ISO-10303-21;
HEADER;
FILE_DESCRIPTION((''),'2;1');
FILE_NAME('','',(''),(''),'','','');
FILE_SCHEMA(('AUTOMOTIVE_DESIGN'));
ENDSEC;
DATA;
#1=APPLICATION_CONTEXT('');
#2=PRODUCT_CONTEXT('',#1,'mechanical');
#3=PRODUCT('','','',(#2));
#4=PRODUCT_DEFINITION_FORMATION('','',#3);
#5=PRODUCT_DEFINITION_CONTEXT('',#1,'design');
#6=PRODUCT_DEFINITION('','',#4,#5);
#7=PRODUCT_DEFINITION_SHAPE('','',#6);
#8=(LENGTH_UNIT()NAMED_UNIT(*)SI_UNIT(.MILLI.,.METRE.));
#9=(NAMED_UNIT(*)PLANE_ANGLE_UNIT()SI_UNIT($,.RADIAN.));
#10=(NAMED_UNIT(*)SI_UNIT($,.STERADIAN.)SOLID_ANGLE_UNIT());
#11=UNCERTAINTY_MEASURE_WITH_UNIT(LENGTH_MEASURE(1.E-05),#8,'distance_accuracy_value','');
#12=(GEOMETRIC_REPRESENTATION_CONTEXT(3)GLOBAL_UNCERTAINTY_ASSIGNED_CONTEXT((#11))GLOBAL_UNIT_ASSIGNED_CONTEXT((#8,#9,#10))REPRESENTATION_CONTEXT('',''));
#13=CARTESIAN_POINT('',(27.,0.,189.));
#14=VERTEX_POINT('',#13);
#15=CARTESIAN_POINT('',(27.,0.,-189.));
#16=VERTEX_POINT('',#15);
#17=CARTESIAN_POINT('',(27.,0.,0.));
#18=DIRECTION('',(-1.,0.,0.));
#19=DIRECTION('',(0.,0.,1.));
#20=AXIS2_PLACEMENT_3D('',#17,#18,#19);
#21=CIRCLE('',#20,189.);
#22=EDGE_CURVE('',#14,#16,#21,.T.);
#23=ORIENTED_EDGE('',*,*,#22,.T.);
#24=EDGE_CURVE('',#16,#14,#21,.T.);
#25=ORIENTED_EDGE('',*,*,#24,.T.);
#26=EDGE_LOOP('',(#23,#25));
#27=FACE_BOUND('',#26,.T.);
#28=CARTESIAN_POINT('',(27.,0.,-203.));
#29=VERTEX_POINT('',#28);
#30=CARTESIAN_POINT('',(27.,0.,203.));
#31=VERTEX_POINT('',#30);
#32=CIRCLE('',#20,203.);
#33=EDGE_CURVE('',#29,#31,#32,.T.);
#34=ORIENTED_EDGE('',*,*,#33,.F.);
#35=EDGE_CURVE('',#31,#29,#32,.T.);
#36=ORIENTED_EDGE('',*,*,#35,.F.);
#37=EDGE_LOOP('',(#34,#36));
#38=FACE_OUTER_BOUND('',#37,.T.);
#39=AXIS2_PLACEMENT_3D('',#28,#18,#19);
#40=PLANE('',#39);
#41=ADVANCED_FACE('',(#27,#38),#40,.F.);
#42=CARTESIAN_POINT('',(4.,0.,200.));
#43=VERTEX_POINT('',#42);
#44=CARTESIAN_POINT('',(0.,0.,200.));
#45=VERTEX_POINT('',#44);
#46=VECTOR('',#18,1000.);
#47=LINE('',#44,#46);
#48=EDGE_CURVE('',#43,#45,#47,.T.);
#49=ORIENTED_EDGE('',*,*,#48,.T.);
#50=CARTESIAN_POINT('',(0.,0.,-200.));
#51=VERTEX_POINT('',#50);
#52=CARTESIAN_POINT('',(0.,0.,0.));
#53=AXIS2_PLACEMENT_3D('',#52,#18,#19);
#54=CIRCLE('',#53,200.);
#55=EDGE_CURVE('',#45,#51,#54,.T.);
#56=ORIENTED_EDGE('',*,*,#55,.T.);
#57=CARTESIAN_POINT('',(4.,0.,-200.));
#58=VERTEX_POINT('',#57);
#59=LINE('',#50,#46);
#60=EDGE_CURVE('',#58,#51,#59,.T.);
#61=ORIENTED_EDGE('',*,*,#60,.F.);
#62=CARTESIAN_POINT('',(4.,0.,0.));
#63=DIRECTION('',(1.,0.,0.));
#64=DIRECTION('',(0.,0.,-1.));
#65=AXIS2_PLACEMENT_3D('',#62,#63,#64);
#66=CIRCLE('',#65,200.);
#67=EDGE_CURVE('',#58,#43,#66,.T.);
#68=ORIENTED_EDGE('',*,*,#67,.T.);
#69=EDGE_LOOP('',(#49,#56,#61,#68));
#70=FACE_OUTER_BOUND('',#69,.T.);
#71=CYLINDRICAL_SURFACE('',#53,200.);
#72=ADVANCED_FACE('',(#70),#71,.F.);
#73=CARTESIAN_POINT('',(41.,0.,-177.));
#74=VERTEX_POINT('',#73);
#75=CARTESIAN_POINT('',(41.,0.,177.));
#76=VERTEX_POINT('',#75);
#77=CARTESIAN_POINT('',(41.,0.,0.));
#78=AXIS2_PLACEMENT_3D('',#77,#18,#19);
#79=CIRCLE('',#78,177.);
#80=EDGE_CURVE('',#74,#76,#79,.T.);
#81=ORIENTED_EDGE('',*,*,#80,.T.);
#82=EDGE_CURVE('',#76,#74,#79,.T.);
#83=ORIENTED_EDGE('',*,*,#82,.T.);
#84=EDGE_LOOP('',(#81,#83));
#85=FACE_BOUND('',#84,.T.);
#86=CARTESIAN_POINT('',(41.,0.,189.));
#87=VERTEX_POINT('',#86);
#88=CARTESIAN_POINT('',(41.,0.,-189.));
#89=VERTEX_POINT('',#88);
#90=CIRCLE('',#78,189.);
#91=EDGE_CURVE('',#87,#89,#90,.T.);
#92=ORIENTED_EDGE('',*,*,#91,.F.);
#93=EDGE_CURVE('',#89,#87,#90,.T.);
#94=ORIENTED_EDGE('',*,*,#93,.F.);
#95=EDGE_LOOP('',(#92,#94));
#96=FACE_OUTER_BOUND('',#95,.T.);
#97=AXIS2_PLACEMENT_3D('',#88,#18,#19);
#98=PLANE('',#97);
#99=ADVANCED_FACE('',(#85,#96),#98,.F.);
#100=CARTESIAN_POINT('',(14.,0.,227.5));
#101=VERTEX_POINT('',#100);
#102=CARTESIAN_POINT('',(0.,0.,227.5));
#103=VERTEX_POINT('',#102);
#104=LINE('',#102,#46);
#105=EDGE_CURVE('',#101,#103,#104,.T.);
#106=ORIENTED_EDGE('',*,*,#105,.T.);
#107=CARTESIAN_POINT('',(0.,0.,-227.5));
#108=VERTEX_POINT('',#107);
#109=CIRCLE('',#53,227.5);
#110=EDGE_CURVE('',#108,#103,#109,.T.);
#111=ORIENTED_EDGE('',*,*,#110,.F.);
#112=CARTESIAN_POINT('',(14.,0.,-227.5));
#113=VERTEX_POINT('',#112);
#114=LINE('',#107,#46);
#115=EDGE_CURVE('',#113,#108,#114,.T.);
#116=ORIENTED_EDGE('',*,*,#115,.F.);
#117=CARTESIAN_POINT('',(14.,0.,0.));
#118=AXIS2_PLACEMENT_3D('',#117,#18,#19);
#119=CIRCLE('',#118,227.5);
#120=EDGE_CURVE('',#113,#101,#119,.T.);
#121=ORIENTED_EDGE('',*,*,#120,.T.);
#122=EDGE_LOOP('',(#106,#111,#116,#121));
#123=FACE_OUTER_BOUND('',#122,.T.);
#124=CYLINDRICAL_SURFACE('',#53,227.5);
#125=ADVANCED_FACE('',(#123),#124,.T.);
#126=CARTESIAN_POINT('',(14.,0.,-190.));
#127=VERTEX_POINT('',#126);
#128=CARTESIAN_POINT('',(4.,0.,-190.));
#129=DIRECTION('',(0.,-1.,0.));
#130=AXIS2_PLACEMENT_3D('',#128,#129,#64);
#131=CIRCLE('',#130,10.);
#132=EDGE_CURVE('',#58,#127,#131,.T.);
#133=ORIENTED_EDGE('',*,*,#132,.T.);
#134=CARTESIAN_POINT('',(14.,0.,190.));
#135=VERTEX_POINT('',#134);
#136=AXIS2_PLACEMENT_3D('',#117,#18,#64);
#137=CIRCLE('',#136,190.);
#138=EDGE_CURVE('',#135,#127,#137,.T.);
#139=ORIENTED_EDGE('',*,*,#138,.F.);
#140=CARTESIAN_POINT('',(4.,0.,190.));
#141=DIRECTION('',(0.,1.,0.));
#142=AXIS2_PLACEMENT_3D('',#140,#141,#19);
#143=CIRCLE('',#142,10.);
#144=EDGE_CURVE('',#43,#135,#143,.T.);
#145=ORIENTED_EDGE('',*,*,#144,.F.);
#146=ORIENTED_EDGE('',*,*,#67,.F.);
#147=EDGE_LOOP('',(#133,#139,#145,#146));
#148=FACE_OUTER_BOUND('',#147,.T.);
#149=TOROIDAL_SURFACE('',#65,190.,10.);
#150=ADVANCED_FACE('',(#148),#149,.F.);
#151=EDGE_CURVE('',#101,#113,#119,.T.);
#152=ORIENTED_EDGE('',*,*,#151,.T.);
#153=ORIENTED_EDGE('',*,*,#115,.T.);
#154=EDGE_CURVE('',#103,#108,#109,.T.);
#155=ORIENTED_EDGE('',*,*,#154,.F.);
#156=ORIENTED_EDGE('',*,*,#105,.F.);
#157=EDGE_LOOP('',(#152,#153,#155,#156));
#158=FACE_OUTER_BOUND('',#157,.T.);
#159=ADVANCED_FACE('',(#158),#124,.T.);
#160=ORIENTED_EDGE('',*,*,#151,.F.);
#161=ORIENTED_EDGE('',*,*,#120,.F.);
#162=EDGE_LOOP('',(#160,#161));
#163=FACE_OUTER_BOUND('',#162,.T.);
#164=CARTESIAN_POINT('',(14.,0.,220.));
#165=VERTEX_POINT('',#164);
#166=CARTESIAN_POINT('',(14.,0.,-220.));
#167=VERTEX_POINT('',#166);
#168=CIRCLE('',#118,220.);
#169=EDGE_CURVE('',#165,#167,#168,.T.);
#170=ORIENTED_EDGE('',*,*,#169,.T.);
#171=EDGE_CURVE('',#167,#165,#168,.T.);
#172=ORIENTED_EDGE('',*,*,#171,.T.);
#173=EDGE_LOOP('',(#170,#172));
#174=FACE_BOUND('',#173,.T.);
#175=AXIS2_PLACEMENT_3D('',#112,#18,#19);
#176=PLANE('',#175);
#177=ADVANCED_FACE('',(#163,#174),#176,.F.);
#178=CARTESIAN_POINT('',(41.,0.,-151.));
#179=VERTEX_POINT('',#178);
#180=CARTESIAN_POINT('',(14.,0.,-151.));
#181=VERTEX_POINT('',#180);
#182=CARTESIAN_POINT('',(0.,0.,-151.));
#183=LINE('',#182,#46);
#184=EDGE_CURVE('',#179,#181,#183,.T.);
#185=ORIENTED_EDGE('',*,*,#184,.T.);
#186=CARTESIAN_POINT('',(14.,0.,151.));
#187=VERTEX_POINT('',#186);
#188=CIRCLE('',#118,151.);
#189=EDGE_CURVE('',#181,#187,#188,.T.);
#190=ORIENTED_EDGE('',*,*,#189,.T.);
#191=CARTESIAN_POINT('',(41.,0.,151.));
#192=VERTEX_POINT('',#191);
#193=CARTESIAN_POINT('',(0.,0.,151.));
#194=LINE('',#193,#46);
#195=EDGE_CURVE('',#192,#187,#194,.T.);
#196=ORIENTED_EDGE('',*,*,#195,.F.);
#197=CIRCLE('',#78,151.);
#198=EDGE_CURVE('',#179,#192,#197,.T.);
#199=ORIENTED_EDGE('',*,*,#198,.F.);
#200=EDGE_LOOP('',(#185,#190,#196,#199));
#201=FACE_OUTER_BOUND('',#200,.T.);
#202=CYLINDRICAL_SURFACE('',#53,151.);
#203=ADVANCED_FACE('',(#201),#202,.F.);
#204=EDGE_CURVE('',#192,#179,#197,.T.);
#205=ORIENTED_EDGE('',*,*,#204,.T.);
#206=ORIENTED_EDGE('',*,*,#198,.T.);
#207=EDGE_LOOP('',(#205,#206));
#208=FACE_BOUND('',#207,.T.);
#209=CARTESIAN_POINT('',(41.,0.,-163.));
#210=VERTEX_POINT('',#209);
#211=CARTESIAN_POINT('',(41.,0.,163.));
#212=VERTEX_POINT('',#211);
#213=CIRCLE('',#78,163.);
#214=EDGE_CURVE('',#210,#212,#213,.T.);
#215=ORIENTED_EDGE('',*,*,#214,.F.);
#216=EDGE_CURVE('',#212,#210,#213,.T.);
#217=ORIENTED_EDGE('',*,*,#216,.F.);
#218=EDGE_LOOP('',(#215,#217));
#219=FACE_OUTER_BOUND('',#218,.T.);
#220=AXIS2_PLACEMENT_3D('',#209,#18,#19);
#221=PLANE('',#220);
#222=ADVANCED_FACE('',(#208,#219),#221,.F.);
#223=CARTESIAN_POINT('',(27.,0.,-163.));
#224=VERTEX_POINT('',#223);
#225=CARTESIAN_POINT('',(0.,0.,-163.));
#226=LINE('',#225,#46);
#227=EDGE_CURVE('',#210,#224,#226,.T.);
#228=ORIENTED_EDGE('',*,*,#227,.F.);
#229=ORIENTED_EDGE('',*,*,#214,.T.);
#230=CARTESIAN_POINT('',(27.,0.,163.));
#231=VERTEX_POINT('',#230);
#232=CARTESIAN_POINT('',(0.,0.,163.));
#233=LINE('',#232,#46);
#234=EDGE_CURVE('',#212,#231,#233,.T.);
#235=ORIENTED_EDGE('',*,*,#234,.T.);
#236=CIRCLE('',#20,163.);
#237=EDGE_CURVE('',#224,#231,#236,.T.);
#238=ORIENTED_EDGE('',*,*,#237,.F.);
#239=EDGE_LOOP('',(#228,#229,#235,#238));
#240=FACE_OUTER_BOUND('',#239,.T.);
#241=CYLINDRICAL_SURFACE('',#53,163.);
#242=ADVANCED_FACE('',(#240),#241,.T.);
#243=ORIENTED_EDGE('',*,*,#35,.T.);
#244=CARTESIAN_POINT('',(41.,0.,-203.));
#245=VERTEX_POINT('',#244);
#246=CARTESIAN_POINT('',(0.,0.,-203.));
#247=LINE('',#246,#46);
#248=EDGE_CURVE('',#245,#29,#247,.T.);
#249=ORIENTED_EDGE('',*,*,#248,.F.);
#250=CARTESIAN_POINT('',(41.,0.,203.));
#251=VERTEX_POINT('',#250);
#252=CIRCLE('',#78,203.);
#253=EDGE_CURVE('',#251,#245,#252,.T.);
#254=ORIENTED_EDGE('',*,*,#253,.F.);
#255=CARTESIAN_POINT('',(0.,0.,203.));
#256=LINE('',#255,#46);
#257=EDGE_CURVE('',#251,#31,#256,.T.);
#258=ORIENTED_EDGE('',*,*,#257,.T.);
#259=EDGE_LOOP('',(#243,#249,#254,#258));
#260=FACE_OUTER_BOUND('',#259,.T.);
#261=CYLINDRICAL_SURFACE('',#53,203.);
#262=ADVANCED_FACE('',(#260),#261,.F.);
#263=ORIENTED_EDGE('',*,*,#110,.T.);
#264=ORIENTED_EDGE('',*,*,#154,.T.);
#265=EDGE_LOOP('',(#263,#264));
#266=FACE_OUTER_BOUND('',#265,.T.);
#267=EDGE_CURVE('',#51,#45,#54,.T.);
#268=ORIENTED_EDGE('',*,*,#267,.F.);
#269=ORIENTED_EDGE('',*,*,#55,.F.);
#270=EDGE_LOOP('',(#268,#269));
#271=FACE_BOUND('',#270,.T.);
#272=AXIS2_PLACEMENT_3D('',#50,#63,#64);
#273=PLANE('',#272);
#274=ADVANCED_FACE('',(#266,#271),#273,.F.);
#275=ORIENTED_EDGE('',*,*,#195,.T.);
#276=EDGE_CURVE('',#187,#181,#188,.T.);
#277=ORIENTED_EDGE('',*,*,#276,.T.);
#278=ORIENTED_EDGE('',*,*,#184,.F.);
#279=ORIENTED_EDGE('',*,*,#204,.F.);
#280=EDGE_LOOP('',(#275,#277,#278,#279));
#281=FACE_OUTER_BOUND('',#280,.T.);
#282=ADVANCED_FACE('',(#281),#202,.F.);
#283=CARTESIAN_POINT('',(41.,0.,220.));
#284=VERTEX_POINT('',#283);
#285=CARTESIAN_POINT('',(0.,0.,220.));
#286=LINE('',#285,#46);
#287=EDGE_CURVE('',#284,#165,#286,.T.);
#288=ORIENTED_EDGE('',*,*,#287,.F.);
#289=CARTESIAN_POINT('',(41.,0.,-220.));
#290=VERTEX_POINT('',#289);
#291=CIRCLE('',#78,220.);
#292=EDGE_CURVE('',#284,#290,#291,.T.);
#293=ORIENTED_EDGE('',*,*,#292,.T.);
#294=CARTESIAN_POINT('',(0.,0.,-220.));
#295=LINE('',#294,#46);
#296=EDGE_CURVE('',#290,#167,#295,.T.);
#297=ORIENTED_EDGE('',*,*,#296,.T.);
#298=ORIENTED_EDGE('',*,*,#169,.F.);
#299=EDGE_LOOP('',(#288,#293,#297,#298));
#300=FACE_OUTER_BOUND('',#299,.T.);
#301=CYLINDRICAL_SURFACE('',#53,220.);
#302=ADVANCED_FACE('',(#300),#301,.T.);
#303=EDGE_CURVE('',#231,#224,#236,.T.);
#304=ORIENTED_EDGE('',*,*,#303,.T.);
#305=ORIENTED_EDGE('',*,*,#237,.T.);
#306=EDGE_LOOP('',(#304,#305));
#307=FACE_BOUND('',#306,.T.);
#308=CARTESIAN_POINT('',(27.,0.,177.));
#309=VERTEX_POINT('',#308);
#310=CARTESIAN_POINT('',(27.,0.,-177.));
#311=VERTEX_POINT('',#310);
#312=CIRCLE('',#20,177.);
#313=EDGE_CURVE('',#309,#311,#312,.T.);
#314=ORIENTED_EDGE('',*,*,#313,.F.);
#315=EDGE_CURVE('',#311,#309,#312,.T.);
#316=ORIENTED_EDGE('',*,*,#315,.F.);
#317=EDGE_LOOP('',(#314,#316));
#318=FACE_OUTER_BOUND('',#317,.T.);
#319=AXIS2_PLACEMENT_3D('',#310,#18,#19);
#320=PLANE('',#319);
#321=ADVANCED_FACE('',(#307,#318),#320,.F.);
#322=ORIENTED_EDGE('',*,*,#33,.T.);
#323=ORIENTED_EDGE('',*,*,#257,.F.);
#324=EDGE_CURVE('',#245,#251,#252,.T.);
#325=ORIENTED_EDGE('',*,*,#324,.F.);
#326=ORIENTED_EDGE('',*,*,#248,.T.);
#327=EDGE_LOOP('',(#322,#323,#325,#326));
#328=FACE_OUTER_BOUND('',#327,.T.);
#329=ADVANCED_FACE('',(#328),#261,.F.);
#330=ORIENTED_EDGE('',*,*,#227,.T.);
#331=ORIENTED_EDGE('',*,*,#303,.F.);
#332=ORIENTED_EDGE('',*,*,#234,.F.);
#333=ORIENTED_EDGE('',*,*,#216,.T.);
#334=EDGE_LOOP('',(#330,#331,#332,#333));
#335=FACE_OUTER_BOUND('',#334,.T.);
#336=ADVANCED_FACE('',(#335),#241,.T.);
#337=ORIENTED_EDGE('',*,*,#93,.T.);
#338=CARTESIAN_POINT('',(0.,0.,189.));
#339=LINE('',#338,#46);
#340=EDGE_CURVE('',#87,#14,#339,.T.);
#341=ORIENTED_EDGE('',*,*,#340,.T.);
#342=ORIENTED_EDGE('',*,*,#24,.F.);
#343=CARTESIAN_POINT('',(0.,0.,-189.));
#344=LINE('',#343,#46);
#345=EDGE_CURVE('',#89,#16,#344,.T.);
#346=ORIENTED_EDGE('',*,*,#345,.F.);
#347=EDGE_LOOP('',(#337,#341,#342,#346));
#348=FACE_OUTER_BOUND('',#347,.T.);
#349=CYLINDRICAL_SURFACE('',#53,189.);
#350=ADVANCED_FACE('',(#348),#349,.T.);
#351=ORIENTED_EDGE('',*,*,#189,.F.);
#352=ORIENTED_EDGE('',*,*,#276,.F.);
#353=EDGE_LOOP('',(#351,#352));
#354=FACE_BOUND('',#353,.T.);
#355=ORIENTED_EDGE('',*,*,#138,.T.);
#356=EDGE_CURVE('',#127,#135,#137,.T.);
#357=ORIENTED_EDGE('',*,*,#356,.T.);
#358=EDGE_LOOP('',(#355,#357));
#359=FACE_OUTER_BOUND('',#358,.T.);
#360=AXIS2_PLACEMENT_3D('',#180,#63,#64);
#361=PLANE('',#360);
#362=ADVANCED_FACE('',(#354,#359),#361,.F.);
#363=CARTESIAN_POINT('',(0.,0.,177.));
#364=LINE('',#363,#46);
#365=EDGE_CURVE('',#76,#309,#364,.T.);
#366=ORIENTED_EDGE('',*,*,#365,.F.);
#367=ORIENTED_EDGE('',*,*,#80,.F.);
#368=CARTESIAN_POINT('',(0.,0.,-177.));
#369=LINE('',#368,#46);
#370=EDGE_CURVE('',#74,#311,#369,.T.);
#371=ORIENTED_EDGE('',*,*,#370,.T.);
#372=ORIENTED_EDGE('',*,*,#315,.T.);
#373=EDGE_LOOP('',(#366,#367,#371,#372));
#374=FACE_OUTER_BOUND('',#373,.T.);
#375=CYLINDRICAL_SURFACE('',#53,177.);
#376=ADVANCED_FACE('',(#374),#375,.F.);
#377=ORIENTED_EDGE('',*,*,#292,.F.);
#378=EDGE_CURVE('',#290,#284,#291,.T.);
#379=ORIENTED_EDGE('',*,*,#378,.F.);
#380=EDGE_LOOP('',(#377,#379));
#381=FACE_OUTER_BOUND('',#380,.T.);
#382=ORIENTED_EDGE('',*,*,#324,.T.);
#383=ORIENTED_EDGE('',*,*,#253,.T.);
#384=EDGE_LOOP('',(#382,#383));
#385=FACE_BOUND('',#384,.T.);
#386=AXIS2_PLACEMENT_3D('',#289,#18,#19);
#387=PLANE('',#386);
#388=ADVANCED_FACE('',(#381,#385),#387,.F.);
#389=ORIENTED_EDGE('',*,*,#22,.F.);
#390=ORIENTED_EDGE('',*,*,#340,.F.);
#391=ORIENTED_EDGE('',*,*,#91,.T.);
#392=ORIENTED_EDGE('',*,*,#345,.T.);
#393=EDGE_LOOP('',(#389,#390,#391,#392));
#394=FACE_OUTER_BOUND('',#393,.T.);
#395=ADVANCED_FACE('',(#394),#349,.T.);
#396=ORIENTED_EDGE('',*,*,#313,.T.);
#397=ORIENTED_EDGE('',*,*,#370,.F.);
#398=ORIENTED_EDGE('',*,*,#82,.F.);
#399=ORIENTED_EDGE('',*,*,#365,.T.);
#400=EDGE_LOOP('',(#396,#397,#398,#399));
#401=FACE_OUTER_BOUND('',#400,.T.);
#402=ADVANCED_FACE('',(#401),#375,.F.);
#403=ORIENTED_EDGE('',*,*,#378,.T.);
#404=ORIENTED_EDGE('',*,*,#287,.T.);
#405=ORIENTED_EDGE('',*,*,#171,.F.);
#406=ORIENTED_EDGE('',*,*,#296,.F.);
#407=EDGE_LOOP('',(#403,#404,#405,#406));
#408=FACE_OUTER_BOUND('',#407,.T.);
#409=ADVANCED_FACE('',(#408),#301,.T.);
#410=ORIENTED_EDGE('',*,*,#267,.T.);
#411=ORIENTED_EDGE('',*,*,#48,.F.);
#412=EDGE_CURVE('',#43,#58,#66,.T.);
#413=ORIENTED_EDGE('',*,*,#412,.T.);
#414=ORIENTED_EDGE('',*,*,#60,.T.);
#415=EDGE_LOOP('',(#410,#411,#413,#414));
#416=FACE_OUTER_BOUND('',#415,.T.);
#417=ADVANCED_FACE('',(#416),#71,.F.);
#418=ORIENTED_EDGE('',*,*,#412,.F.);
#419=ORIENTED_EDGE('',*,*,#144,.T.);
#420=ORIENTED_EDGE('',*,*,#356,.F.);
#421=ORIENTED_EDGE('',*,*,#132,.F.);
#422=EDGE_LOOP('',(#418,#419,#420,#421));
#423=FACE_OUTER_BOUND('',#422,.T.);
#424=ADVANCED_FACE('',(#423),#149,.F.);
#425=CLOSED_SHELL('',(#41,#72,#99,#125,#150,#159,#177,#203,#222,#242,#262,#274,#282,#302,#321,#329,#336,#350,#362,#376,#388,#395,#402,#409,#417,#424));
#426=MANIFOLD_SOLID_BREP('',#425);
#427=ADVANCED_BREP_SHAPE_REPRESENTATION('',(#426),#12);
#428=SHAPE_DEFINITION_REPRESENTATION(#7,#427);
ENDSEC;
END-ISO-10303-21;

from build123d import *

# Parameters (mm, degrees)
FILLET1_R = 10


with BuildPart() as part:
    # Sketch1 → Revolve1 (revolve)
    with BuildSketch(Plane(origin=(0, 0, 0), x_dir=(1, 0, 0), z_dir=(0, 1, 0)), mode=Mode.PRIVATE) as revolve1_sk:
        Polygon((0, 200), (0, 227.5), (14, 227.5), (14, 220), (41, 220), (41, 203), (27, 203), (27, 189), (41, 189), (41, 177), (27, 177), (27, 163), (41, 163), (41, 151), (14, 151), (14, 200), align=None)
    revolve(revolve1_sk.sketch.rotate(Axis((0, 0, 0), (1, 0, 0)), 180), axis=Axis((0, 0, 0), (1, 0, 0)))

    # Fillet1
    fillet1_edges = [part.edges().sort_by_distance(p)[0] for p in [
        (14, 0, -200),
    ]]
    fillet(fillet1_edges, radius=FILLET1_R)


solid = part.part
